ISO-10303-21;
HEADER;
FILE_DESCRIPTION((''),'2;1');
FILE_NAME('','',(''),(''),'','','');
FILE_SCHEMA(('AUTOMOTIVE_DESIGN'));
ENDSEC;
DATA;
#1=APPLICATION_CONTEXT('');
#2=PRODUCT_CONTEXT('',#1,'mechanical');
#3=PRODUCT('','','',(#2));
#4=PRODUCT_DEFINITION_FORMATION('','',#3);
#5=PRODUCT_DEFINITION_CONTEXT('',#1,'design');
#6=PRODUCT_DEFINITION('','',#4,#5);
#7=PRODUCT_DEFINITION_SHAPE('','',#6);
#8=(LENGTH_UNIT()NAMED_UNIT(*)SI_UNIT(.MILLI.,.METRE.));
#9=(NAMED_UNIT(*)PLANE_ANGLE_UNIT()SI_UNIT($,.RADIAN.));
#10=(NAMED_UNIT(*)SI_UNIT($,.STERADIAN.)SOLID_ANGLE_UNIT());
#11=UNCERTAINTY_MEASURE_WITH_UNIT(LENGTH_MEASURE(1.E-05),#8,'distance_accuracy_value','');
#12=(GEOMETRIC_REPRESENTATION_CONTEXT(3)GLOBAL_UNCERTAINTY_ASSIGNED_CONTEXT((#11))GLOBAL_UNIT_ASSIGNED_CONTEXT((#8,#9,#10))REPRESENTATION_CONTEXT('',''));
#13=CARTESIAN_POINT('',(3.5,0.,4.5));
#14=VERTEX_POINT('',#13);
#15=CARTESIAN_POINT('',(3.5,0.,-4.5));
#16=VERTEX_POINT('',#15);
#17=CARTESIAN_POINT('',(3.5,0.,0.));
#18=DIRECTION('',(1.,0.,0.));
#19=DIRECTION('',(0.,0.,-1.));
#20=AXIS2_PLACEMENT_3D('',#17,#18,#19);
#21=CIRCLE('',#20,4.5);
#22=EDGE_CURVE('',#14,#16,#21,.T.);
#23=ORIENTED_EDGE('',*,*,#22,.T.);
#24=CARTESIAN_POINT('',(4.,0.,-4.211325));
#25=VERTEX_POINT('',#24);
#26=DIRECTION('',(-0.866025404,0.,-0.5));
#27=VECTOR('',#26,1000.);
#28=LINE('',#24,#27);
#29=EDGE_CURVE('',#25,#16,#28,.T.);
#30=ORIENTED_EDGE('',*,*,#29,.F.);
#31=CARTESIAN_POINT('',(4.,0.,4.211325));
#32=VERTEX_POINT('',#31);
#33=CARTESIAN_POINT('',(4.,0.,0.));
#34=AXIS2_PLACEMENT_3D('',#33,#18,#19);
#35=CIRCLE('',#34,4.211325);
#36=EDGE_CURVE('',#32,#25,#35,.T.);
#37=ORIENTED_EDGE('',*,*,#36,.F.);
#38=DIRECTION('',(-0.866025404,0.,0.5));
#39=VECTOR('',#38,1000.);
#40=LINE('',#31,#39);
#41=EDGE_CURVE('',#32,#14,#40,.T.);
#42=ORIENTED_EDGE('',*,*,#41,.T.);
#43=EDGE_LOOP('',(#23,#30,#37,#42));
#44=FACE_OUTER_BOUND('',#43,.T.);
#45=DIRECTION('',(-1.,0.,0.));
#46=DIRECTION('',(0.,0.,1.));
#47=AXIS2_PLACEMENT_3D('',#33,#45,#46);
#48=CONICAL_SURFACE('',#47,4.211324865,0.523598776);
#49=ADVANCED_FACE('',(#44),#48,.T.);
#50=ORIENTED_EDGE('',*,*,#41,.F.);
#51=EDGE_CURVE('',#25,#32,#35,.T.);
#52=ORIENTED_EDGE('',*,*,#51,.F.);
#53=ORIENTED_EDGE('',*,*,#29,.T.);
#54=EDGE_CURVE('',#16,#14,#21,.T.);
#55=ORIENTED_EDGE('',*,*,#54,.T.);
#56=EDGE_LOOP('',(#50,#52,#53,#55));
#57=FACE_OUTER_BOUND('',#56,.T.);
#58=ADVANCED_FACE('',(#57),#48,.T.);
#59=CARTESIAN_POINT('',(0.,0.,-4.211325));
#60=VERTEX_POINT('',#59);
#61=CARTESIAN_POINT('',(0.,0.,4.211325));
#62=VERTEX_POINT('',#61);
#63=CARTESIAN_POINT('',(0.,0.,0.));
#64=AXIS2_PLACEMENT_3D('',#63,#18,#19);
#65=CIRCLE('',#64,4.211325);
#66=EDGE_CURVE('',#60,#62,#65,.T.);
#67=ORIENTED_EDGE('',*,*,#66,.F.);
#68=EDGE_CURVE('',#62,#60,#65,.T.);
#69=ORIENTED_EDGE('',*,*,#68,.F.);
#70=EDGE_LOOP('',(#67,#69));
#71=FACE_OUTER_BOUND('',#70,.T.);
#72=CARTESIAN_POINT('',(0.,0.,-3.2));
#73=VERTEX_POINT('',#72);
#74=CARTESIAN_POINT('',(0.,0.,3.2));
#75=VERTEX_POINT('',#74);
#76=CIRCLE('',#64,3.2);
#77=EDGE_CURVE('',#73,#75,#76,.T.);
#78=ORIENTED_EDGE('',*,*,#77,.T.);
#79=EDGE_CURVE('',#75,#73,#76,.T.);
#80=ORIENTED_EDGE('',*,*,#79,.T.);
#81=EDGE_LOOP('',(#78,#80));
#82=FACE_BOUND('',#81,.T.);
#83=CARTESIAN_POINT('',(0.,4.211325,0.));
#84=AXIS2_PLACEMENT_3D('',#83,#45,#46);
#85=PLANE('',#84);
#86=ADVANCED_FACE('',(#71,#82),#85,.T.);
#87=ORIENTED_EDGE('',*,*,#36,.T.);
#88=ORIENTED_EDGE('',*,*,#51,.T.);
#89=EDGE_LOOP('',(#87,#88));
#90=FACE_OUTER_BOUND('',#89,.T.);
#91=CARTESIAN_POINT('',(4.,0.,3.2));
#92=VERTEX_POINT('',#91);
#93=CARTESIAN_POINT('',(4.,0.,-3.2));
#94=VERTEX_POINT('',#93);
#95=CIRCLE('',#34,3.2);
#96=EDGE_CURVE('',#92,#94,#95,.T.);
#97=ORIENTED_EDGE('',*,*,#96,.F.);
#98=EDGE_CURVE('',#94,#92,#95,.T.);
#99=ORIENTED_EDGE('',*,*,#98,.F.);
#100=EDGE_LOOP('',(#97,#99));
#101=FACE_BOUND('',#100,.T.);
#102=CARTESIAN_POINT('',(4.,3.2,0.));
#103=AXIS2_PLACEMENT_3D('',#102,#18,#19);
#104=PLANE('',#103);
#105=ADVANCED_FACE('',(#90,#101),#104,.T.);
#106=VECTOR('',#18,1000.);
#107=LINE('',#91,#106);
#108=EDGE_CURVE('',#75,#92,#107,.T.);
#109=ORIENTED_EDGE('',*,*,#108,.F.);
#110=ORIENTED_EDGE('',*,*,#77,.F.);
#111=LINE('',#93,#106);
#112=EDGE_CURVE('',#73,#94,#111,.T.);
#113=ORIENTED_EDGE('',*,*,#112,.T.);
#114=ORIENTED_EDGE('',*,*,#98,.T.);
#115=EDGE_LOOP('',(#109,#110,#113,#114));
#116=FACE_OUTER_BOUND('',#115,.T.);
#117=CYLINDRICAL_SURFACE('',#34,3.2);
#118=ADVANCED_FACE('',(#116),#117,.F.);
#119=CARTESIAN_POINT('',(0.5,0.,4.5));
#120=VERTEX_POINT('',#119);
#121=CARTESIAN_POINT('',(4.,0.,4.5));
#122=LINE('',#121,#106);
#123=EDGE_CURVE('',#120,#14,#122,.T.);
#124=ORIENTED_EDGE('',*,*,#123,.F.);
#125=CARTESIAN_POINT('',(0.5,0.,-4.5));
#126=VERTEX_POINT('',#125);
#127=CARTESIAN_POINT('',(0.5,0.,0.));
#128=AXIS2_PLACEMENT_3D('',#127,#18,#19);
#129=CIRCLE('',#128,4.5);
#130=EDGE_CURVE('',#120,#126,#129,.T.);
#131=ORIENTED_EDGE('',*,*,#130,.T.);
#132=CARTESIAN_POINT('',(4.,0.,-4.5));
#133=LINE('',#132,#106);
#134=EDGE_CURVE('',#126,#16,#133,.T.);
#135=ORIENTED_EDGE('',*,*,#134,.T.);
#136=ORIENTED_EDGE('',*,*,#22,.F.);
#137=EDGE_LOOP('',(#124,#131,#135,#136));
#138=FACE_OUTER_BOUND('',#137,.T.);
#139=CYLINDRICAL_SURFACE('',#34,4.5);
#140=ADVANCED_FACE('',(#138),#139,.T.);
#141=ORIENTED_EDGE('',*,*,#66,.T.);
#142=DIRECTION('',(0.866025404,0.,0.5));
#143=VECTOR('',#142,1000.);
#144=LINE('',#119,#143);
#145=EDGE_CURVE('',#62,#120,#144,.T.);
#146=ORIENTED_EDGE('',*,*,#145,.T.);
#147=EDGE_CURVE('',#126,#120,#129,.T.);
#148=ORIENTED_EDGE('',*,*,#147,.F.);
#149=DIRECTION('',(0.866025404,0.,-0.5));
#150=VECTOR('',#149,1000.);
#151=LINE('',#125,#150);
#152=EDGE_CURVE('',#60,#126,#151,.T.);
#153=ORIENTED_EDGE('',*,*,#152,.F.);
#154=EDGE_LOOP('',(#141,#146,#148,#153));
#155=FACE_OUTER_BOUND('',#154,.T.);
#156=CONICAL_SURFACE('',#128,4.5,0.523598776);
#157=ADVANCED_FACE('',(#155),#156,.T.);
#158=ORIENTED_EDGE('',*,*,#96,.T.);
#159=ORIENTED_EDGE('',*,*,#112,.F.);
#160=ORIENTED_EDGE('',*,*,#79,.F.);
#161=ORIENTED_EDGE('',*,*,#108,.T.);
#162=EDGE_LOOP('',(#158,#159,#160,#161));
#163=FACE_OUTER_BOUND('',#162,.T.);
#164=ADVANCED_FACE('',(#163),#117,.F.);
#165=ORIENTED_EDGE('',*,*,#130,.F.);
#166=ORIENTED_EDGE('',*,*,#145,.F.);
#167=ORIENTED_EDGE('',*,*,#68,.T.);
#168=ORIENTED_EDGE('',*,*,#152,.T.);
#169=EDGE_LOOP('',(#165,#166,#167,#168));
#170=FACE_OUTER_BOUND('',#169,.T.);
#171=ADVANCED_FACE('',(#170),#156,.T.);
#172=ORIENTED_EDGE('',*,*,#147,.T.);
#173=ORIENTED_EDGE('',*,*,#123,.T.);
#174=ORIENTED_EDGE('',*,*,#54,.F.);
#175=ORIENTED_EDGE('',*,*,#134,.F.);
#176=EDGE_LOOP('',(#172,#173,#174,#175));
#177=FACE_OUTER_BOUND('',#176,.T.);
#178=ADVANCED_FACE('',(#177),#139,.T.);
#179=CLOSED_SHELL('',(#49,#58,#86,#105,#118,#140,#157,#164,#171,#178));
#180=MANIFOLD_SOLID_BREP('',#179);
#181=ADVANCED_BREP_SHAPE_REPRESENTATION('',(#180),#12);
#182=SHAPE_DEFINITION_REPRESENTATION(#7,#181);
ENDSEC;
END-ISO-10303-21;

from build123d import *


with BuildPart() as part:
    # Sketch1 → Revolve1 (revolve)
    with BuildSketch(Plane.XY, mode=Mode.PRIVATE) as revolve1_sk:
        Polygon((0, 3.2), (4, 3.2), (4, 4.211324865), (3.5, 4.5), (0.5, 4.5), (0, 4.211324865), align=None)
    revolve(revolve1_sk.sketch.rotate(Axis((4, 0, 0), (-1, 0, 0)), 90), axis=Axis((4, 0, 0), (-1, 0, 0)))


solid = part.part
